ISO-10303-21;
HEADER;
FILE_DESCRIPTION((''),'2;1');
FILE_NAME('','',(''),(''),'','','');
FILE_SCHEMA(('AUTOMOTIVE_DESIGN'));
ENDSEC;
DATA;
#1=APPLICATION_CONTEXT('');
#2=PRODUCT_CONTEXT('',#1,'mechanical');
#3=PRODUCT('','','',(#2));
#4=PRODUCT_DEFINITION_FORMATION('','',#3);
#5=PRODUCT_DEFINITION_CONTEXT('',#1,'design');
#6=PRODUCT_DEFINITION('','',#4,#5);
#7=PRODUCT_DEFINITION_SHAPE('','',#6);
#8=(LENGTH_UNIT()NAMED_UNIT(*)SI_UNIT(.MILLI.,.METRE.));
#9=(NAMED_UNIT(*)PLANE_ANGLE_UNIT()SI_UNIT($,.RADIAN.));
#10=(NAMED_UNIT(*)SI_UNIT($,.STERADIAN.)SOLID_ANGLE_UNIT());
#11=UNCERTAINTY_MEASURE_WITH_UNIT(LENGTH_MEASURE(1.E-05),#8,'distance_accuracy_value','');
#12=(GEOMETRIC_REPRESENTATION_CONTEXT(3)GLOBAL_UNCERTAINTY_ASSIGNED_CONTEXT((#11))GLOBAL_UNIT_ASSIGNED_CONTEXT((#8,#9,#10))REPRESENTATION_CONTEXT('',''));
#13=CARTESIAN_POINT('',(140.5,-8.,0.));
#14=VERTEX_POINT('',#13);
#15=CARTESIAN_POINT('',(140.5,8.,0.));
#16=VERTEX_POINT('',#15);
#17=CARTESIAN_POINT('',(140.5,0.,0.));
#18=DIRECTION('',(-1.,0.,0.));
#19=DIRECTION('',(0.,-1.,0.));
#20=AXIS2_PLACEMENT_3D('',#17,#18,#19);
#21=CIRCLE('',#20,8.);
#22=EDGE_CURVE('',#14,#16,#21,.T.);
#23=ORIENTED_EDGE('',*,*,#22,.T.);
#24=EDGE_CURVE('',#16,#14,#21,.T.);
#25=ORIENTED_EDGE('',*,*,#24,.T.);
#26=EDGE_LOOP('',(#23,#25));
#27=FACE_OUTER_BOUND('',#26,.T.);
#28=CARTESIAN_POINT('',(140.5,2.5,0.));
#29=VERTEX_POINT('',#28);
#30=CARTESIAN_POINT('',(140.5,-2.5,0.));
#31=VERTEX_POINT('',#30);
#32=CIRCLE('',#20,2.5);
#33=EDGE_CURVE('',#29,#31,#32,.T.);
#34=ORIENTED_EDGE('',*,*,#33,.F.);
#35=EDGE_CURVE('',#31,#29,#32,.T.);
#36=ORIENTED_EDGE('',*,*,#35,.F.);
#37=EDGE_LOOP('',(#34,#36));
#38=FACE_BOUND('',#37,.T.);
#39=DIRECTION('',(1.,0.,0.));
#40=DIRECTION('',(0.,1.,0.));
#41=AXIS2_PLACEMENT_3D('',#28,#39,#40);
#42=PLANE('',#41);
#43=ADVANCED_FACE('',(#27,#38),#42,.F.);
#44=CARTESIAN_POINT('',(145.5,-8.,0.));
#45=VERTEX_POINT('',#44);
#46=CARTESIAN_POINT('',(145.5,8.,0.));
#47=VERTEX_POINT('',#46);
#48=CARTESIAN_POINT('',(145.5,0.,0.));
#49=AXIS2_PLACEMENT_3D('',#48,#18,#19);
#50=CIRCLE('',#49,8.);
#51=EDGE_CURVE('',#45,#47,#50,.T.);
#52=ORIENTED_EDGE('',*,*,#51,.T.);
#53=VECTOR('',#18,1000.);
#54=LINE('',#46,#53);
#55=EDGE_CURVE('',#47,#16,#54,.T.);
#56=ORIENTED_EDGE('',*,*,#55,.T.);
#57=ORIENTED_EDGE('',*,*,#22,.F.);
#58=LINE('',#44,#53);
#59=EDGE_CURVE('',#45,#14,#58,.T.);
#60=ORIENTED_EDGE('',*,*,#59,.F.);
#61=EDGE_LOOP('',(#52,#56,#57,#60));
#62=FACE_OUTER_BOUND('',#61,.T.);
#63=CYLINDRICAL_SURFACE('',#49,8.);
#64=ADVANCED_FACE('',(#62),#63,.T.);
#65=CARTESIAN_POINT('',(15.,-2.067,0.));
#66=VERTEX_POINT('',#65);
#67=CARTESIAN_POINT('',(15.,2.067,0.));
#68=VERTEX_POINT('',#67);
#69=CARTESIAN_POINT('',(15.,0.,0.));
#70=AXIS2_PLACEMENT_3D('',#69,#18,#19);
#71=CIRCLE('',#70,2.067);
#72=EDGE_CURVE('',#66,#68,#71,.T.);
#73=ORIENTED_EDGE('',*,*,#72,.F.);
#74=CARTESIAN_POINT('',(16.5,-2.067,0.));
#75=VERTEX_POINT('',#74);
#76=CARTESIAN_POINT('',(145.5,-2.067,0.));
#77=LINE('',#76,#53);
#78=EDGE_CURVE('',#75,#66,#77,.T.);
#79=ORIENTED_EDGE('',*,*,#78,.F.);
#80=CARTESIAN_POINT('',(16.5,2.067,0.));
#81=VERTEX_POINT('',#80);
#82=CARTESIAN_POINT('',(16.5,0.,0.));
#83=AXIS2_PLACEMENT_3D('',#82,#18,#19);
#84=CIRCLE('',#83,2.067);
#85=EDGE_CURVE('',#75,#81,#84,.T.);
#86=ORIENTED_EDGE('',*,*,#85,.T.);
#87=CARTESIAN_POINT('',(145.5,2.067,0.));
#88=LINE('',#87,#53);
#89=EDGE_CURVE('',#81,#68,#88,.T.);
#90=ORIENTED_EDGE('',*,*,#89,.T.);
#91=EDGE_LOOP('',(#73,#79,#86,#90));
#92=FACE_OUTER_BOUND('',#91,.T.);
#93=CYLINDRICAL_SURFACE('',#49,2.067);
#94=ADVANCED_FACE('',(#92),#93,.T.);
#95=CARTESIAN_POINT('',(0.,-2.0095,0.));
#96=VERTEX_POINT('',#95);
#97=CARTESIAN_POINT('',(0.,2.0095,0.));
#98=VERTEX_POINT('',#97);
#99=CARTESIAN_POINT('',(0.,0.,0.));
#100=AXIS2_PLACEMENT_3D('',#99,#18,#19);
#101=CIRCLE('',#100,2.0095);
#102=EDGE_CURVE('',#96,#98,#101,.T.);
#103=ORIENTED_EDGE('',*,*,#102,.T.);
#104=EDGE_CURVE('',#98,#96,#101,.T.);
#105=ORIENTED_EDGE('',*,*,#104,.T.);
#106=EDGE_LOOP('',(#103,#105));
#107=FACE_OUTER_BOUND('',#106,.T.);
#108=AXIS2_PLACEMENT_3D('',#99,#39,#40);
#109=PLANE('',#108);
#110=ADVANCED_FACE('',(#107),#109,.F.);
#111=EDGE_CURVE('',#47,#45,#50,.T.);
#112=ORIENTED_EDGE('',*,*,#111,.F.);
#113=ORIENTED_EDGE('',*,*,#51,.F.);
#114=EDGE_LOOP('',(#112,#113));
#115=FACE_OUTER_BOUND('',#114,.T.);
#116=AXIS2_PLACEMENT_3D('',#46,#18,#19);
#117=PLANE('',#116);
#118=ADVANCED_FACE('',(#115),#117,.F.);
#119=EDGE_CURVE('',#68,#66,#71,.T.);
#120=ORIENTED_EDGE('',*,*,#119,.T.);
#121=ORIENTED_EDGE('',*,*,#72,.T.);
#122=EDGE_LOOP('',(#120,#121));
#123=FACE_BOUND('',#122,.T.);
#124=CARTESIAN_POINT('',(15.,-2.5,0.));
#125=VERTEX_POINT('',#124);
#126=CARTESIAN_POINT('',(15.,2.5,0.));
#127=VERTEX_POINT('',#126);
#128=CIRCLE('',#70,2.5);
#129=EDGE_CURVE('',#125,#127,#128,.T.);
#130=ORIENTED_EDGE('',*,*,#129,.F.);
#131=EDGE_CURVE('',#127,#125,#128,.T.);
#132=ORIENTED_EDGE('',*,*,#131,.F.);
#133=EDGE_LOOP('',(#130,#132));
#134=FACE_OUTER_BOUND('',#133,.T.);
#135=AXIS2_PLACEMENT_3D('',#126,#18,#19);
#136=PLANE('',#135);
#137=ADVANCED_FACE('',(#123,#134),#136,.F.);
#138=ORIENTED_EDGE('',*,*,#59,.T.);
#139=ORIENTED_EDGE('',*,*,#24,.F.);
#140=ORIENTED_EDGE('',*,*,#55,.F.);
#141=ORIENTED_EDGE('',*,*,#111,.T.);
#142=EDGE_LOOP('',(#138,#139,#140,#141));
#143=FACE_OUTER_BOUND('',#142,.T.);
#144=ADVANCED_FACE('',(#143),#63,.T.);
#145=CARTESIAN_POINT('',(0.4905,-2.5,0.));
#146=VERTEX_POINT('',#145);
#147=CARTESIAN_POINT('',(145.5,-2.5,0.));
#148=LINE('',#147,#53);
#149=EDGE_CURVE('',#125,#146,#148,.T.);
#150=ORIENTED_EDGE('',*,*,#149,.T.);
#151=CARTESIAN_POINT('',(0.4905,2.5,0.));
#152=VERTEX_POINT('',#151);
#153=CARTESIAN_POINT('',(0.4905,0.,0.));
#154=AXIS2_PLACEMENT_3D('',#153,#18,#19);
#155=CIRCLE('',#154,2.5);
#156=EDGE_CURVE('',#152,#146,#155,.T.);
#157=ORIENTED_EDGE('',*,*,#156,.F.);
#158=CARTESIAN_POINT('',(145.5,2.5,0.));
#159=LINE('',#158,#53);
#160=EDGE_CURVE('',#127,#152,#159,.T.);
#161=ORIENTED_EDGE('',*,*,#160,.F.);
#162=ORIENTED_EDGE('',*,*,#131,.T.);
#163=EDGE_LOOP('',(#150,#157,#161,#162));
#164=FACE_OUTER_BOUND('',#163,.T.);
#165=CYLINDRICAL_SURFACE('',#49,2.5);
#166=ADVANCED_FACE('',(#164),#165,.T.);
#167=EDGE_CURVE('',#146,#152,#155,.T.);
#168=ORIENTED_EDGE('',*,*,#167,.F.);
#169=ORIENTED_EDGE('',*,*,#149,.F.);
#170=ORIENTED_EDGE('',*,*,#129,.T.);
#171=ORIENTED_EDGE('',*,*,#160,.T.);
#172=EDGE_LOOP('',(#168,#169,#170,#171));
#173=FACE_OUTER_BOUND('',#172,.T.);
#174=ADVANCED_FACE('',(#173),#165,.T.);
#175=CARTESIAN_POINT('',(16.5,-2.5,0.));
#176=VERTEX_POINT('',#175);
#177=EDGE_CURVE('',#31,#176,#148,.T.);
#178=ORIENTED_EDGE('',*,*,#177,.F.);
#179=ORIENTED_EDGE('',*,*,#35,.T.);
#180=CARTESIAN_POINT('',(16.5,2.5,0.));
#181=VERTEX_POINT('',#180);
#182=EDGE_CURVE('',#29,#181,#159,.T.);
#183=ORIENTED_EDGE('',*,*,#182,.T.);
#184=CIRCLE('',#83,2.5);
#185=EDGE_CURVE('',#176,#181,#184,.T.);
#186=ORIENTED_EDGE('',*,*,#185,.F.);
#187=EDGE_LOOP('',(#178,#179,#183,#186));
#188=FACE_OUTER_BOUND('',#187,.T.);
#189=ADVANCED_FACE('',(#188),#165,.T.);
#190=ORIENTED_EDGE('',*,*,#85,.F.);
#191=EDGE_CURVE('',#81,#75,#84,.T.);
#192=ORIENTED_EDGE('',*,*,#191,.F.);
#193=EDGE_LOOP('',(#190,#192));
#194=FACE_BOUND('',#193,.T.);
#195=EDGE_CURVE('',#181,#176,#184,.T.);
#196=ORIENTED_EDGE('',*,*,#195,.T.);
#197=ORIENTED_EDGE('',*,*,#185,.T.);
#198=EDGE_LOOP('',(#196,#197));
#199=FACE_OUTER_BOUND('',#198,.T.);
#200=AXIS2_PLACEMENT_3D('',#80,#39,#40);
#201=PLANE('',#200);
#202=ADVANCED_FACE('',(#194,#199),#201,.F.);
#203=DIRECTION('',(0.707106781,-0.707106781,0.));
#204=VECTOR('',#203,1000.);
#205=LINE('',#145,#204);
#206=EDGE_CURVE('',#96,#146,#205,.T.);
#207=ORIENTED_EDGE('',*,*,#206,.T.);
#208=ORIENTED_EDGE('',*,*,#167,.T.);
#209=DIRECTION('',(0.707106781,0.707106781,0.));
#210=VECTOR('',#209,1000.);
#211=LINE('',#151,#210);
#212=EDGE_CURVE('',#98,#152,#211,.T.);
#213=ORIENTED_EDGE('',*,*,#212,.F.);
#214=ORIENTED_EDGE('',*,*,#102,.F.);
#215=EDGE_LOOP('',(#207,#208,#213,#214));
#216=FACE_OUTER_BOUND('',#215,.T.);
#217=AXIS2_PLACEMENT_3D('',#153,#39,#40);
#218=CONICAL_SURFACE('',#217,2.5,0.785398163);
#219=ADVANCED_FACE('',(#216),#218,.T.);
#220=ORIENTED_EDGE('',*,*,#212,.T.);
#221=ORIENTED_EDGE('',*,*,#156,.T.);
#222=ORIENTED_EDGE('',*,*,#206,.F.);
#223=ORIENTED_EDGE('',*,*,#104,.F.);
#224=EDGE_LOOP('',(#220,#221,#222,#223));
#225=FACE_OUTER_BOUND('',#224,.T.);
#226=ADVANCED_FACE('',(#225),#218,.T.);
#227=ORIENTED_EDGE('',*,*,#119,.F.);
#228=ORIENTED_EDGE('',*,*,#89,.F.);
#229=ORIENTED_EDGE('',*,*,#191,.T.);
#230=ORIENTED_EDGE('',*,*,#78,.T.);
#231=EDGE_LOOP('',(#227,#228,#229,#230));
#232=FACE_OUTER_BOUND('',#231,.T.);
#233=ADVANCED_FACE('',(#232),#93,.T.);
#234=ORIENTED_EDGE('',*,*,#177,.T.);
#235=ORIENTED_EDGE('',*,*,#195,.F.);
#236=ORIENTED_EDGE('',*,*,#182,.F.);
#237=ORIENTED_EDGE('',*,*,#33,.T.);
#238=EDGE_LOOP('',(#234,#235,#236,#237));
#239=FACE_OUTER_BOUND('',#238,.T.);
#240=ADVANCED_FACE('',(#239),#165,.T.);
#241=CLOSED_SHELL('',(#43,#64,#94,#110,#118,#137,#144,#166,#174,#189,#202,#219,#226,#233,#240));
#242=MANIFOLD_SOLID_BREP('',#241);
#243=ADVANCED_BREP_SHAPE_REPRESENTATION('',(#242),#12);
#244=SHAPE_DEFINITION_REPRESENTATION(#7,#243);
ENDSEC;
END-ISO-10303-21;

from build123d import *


with BuildPart() as part:
    # Sketch1 → Revolve1 (revolve)
    with BuildSketch(Plane.XY, mode=Mode.PRIVATE) as revolve1_sk:
        Polygon((0, 0), (0, 2.0095), (0.4905, 2.5), (15, 2.5), (15, 2.067), (16.5, 2.067), (16.5, 2.5), (140.5, 2.5), (140.5, 8), (145.5, 8), (145.5, 0), align=None)
    revolve(revolve1_sk.sketch.rotate(Axis((145.5, 0, 0), (-1, 0, 0)), 180), axis=Axis((145.5, 0, 0), (-1, 0, 0)))


solid = part.part
